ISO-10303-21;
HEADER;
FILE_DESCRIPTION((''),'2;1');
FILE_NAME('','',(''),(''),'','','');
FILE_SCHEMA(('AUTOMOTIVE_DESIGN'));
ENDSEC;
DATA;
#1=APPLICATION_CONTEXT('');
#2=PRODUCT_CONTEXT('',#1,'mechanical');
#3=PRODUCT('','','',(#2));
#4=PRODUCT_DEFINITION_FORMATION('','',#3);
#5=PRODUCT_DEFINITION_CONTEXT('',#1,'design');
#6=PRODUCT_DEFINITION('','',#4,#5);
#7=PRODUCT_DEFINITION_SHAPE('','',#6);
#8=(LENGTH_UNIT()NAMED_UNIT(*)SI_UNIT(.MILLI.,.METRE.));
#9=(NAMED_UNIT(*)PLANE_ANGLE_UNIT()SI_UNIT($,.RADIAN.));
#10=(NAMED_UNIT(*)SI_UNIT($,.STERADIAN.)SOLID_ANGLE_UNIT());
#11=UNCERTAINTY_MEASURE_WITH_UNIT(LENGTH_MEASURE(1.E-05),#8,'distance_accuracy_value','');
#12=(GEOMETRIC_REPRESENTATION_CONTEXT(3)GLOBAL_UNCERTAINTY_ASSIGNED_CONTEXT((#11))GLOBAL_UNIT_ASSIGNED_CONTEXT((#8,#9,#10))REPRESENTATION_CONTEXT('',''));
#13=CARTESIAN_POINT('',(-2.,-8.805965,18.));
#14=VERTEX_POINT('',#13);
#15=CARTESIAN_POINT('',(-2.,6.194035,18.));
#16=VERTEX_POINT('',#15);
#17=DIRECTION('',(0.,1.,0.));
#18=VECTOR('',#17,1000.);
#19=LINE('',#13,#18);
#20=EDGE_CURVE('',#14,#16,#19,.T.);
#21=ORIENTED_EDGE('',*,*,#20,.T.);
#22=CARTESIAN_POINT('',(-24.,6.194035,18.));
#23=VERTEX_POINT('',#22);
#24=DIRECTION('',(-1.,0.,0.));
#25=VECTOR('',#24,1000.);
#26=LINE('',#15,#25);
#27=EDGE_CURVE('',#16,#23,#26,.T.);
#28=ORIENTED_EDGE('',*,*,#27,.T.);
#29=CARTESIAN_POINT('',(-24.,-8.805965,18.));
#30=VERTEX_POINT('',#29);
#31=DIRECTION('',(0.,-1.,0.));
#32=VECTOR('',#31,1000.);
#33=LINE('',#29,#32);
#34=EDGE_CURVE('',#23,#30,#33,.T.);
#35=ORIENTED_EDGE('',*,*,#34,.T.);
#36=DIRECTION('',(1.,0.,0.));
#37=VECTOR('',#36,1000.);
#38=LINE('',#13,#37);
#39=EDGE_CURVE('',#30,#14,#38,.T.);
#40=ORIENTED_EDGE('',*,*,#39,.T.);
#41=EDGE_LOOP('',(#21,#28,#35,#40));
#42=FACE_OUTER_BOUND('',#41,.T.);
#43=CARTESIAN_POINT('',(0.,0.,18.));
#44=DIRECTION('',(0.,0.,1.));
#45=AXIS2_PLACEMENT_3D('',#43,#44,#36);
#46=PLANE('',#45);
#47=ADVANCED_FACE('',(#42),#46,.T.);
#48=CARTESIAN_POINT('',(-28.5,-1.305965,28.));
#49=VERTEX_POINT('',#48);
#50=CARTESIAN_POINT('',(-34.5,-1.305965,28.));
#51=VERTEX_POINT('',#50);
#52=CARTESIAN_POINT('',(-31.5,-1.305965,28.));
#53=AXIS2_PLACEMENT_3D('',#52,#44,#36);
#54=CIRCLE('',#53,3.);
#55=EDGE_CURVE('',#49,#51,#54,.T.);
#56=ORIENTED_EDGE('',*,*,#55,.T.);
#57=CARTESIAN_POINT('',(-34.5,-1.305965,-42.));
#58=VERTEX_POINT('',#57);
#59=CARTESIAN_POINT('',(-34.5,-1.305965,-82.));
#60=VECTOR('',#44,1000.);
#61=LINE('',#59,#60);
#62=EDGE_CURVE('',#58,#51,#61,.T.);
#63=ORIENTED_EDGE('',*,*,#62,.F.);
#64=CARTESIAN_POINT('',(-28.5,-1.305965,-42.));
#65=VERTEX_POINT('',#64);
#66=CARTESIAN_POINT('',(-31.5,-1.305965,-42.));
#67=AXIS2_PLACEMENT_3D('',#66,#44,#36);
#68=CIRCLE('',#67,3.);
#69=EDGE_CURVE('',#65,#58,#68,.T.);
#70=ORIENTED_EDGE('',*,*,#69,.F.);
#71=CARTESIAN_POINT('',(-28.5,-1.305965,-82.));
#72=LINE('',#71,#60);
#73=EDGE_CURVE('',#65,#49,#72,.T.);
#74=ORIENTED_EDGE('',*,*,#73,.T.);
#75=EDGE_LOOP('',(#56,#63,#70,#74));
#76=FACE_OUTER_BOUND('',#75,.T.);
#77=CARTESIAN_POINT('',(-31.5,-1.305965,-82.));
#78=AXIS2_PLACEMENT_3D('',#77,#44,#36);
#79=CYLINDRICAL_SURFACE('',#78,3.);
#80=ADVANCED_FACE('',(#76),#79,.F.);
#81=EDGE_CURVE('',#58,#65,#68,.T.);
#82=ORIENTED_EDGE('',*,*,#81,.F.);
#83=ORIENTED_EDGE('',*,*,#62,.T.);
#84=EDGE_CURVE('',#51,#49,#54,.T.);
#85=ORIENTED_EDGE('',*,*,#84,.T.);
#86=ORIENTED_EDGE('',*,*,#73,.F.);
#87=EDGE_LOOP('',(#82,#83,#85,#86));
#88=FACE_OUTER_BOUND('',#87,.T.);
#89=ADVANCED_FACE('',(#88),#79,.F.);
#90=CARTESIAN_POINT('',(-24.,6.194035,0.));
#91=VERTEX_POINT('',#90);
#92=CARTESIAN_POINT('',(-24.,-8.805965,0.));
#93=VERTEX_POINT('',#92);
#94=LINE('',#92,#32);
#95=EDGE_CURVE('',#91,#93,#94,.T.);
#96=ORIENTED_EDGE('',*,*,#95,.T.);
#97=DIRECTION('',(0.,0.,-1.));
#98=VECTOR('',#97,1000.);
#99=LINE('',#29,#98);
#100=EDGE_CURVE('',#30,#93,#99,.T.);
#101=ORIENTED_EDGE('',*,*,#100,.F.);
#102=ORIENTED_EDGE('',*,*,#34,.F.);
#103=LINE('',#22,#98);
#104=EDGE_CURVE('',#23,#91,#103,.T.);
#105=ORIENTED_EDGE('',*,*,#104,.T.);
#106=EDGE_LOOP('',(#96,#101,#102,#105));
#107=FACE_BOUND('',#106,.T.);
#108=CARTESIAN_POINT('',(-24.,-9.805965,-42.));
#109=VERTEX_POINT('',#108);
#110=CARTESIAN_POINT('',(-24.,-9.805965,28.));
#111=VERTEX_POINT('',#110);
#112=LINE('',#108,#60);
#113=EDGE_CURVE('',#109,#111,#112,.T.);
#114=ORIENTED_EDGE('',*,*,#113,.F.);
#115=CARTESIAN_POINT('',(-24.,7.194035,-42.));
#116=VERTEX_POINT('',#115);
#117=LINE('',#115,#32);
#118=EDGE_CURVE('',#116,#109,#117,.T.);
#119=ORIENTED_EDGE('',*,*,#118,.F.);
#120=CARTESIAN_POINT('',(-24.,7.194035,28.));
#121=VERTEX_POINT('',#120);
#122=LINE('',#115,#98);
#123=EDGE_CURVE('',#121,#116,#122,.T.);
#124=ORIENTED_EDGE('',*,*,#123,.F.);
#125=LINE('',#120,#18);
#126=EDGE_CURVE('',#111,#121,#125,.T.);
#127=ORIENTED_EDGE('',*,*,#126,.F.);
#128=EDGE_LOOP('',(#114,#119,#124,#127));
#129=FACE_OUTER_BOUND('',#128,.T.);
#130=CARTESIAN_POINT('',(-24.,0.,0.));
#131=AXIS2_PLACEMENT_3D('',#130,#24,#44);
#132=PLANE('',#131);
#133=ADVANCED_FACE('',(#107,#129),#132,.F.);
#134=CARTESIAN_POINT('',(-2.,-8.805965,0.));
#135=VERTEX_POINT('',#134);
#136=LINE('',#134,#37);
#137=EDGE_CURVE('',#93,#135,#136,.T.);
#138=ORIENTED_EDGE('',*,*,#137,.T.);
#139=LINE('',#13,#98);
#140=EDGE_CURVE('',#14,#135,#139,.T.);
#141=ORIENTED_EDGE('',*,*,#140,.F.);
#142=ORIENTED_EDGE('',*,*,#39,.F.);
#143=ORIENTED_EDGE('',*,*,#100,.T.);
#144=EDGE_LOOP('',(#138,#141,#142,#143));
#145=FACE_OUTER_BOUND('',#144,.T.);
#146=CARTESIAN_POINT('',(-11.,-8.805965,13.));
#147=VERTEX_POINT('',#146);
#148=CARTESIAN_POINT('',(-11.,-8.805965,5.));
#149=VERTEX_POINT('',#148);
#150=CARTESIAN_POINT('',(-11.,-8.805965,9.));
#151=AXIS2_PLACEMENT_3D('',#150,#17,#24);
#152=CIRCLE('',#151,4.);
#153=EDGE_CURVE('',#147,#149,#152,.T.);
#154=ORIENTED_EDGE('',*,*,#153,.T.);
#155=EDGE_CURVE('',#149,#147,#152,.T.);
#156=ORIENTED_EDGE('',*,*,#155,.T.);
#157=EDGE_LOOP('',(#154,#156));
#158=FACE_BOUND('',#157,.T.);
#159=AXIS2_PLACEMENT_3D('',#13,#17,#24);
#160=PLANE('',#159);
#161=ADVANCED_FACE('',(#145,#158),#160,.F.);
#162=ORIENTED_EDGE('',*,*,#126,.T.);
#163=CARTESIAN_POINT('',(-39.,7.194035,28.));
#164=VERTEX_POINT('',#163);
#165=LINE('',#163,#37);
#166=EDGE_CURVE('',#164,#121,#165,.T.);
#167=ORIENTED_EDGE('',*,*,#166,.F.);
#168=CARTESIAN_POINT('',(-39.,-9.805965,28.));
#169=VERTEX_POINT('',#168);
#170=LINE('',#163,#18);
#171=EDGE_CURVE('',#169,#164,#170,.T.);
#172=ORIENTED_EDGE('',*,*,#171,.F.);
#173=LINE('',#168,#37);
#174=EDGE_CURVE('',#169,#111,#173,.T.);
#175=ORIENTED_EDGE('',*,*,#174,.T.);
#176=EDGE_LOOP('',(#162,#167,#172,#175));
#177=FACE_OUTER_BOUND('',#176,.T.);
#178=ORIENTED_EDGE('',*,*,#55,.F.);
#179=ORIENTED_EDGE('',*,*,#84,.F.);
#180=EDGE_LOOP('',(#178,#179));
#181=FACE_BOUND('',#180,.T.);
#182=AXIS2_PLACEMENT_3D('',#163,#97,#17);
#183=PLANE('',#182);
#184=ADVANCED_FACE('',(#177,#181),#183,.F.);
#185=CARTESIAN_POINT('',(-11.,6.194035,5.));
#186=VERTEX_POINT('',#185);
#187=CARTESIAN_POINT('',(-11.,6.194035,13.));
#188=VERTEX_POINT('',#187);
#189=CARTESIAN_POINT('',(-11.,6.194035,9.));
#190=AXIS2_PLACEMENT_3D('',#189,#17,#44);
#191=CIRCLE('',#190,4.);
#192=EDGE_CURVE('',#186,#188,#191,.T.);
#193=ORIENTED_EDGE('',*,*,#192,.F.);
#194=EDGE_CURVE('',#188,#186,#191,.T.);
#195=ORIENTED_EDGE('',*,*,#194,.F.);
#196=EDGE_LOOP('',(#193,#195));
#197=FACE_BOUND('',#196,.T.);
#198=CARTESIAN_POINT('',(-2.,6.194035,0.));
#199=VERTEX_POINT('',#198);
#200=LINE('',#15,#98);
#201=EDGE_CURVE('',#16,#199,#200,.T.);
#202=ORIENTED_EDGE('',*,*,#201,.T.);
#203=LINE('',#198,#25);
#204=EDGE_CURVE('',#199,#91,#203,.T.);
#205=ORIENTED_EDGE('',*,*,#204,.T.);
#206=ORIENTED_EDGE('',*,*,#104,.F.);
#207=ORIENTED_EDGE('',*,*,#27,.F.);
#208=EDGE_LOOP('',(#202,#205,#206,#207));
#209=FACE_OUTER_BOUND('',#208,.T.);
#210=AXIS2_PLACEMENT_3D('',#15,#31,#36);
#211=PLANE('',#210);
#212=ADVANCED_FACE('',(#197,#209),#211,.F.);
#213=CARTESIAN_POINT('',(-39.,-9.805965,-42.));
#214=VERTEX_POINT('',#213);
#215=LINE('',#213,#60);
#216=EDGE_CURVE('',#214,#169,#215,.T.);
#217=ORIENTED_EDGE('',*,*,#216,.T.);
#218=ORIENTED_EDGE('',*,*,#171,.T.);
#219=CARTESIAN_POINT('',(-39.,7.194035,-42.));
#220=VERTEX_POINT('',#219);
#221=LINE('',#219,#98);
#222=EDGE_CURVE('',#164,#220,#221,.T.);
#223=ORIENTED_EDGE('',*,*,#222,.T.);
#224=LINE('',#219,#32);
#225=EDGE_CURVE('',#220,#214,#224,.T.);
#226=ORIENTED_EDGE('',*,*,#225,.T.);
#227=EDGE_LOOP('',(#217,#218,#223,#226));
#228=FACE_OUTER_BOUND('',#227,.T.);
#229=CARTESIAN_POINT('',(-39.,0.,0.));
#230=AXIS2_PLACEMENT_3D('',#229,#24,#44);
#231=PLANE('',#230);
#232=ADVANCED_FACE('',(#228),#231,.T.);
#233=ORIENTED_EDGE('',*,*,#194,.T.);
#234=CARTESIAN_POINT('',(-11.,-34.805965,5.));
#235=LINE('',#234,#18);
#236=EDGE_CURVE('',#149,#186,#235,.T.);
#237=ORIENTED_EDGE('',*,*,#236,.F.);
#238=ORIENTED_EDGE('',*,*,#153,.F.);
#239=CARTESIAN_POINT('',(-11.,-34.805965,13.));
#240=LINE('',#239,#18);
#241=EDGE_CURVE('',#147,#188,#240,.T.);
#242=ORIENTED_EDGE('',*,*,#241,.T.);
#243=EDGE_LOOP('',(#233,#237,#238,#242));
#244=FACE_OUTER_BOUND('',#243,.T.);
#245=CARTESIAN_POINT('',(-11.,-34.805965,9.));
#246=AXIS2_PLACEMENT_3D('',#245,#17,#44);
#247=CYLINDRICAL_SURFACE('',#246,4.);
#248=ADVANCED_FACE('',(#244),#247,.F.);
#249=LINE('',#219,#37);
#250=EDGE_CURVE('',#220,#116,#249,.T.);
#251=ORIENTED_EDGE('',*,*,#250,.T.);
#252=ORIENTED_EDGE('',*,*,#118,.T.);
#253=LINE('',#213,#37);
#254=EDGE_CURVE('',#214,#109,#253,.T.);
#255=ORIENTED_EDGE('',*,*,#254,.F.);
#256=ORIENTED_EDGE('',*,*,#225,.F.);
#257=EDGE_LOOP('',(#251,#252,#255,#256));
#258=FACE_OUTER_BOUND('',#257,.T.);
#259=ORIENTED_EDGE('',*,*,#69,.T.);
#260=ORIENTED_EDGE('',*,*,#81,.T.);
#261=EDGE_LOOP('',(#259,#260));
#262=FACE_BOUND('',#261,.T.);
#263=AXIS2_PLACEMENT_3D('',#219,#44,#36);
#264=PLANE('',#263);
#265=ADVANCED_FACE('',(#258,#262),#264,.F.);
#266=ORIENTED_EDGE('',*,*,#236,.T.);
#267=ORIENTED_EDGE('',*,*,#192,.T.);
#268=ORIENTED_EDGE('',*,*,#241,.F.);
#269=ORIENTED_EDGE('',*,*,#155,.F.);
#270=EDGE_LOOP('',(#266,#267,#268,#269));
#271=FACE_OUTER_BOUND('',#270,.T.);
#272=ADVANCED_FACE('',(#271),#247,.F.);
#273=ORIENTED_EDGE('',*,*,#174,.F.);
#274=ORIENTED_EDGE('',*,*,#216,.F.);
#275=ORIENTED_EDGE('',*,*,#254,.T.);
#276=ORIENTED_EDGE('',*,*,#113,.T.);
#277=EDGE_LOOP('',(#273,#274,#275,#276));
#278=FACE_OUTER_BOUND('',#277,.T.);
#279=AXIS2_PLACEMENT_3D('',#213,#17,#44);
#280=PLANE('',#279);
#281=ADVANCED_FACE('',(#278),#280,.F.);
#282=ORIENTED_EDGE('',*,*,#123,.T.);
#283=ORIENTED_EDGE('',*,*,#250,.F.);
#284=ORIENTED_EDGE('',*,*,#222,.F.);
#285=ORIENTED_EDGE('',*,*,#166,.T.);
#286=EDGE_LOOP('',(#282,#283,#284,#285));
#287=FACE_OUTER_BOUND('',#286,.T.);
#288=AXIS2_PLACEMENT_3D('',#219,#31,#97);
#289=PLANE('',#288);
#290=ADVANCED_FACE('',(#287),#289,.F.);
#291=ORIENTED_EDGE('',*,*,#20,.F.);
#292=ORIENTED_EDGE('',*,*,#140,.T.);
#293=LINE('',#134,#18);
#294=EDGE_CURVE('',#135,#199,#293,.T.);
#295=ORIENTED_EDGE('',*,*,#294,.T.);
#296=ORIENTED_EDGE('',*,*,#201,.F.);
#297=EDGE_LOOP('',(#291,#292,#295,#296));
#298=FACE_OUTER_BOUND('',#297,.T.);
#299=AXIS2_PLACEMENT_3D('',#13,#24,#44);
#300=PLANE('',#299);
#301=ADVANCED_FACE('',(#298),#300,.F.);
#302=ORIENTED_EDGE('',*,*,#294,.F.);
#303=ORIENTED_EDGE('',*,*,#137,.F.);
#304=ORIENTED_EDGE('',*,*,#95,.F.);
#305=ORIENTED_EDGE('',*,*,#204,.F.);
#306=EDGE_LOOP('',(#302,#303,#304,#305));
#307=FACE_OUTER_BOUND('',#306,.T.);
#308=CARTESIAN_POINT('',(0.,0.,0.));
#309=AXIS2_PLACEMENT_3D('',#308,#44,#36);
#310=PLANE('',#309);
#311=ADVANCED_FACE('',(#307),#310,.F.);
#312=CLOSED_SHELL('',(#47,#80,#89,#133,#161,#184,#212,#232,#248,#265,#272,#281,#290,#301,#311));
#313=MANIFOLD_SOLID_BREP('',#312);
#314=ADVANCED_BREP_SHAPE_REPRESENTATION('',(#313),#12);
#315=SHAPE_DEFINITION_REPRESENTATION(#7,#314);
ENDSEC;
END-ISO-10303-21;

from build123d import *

# Parameters (mm, degrees)
SKETCH1_W           = 22
SKETCH1_H           = 15
BOSS_EXTRUDE1_DEPTH = 18
SKETCH2_W           = 70
SKETCH2_H           = 17
BOSS_EXTRUDE2_DEPTH = 15
SKETCH4_R           = 3
CUT_EXTRUDE2_DEPTH  = 110
SKETCH3_R           = 4
CUT_EXTRUDE4_DEPTH  = 41


with BuildPart() as part:
    # Sketch1 → Boss-Extrude1 (new body)
    with BuildSketch(Plane.XY):
        with Locations((-13, -1.305964762)):
            Rectangle(SKETCH1_W, SKETCH1_H)
    extrude(amount=BOSS_EXTRUDE1_DEPTH)

    # Sketch2 → Boss-Extrude2 (add)
    with BuildSketch(Plane.ZY.offset(24)):
        with Locations((-7, -1.305964762)):
            Rectangle(SKETCH2_W, SKETCH2_H)
    extrude(amount=BOSS_EXTRUDE2_DEPTH)

    # Sketch4 → Cut-Extrude2 (cut)
    with BuildSketch(Plane.XY.offset(28)):
        with Locations((-31.5, -1.305964762)):
            Circle(SKETCH4_R)
    extrude(amount=-CUT_EXTRUDE2_DEPTH, mode=Mode.SUBTRACT)

    # Sketch3 → Cut-Extrude4 (cut)
    with BuildSketch(Plane(origin=(0, 6.194035238, 0), x_dir=(1, 0, 0), z_dir=(0, 1, 0))):
        with Locations(Location((-11, -9, 0), (0, 0, 270))):
            Circle(SKETCH3_R)
    extrude(amount=-CUT_EXTRUDE4_DEPTH, mode=Mode.SUBTRACT)


solid = part.part
